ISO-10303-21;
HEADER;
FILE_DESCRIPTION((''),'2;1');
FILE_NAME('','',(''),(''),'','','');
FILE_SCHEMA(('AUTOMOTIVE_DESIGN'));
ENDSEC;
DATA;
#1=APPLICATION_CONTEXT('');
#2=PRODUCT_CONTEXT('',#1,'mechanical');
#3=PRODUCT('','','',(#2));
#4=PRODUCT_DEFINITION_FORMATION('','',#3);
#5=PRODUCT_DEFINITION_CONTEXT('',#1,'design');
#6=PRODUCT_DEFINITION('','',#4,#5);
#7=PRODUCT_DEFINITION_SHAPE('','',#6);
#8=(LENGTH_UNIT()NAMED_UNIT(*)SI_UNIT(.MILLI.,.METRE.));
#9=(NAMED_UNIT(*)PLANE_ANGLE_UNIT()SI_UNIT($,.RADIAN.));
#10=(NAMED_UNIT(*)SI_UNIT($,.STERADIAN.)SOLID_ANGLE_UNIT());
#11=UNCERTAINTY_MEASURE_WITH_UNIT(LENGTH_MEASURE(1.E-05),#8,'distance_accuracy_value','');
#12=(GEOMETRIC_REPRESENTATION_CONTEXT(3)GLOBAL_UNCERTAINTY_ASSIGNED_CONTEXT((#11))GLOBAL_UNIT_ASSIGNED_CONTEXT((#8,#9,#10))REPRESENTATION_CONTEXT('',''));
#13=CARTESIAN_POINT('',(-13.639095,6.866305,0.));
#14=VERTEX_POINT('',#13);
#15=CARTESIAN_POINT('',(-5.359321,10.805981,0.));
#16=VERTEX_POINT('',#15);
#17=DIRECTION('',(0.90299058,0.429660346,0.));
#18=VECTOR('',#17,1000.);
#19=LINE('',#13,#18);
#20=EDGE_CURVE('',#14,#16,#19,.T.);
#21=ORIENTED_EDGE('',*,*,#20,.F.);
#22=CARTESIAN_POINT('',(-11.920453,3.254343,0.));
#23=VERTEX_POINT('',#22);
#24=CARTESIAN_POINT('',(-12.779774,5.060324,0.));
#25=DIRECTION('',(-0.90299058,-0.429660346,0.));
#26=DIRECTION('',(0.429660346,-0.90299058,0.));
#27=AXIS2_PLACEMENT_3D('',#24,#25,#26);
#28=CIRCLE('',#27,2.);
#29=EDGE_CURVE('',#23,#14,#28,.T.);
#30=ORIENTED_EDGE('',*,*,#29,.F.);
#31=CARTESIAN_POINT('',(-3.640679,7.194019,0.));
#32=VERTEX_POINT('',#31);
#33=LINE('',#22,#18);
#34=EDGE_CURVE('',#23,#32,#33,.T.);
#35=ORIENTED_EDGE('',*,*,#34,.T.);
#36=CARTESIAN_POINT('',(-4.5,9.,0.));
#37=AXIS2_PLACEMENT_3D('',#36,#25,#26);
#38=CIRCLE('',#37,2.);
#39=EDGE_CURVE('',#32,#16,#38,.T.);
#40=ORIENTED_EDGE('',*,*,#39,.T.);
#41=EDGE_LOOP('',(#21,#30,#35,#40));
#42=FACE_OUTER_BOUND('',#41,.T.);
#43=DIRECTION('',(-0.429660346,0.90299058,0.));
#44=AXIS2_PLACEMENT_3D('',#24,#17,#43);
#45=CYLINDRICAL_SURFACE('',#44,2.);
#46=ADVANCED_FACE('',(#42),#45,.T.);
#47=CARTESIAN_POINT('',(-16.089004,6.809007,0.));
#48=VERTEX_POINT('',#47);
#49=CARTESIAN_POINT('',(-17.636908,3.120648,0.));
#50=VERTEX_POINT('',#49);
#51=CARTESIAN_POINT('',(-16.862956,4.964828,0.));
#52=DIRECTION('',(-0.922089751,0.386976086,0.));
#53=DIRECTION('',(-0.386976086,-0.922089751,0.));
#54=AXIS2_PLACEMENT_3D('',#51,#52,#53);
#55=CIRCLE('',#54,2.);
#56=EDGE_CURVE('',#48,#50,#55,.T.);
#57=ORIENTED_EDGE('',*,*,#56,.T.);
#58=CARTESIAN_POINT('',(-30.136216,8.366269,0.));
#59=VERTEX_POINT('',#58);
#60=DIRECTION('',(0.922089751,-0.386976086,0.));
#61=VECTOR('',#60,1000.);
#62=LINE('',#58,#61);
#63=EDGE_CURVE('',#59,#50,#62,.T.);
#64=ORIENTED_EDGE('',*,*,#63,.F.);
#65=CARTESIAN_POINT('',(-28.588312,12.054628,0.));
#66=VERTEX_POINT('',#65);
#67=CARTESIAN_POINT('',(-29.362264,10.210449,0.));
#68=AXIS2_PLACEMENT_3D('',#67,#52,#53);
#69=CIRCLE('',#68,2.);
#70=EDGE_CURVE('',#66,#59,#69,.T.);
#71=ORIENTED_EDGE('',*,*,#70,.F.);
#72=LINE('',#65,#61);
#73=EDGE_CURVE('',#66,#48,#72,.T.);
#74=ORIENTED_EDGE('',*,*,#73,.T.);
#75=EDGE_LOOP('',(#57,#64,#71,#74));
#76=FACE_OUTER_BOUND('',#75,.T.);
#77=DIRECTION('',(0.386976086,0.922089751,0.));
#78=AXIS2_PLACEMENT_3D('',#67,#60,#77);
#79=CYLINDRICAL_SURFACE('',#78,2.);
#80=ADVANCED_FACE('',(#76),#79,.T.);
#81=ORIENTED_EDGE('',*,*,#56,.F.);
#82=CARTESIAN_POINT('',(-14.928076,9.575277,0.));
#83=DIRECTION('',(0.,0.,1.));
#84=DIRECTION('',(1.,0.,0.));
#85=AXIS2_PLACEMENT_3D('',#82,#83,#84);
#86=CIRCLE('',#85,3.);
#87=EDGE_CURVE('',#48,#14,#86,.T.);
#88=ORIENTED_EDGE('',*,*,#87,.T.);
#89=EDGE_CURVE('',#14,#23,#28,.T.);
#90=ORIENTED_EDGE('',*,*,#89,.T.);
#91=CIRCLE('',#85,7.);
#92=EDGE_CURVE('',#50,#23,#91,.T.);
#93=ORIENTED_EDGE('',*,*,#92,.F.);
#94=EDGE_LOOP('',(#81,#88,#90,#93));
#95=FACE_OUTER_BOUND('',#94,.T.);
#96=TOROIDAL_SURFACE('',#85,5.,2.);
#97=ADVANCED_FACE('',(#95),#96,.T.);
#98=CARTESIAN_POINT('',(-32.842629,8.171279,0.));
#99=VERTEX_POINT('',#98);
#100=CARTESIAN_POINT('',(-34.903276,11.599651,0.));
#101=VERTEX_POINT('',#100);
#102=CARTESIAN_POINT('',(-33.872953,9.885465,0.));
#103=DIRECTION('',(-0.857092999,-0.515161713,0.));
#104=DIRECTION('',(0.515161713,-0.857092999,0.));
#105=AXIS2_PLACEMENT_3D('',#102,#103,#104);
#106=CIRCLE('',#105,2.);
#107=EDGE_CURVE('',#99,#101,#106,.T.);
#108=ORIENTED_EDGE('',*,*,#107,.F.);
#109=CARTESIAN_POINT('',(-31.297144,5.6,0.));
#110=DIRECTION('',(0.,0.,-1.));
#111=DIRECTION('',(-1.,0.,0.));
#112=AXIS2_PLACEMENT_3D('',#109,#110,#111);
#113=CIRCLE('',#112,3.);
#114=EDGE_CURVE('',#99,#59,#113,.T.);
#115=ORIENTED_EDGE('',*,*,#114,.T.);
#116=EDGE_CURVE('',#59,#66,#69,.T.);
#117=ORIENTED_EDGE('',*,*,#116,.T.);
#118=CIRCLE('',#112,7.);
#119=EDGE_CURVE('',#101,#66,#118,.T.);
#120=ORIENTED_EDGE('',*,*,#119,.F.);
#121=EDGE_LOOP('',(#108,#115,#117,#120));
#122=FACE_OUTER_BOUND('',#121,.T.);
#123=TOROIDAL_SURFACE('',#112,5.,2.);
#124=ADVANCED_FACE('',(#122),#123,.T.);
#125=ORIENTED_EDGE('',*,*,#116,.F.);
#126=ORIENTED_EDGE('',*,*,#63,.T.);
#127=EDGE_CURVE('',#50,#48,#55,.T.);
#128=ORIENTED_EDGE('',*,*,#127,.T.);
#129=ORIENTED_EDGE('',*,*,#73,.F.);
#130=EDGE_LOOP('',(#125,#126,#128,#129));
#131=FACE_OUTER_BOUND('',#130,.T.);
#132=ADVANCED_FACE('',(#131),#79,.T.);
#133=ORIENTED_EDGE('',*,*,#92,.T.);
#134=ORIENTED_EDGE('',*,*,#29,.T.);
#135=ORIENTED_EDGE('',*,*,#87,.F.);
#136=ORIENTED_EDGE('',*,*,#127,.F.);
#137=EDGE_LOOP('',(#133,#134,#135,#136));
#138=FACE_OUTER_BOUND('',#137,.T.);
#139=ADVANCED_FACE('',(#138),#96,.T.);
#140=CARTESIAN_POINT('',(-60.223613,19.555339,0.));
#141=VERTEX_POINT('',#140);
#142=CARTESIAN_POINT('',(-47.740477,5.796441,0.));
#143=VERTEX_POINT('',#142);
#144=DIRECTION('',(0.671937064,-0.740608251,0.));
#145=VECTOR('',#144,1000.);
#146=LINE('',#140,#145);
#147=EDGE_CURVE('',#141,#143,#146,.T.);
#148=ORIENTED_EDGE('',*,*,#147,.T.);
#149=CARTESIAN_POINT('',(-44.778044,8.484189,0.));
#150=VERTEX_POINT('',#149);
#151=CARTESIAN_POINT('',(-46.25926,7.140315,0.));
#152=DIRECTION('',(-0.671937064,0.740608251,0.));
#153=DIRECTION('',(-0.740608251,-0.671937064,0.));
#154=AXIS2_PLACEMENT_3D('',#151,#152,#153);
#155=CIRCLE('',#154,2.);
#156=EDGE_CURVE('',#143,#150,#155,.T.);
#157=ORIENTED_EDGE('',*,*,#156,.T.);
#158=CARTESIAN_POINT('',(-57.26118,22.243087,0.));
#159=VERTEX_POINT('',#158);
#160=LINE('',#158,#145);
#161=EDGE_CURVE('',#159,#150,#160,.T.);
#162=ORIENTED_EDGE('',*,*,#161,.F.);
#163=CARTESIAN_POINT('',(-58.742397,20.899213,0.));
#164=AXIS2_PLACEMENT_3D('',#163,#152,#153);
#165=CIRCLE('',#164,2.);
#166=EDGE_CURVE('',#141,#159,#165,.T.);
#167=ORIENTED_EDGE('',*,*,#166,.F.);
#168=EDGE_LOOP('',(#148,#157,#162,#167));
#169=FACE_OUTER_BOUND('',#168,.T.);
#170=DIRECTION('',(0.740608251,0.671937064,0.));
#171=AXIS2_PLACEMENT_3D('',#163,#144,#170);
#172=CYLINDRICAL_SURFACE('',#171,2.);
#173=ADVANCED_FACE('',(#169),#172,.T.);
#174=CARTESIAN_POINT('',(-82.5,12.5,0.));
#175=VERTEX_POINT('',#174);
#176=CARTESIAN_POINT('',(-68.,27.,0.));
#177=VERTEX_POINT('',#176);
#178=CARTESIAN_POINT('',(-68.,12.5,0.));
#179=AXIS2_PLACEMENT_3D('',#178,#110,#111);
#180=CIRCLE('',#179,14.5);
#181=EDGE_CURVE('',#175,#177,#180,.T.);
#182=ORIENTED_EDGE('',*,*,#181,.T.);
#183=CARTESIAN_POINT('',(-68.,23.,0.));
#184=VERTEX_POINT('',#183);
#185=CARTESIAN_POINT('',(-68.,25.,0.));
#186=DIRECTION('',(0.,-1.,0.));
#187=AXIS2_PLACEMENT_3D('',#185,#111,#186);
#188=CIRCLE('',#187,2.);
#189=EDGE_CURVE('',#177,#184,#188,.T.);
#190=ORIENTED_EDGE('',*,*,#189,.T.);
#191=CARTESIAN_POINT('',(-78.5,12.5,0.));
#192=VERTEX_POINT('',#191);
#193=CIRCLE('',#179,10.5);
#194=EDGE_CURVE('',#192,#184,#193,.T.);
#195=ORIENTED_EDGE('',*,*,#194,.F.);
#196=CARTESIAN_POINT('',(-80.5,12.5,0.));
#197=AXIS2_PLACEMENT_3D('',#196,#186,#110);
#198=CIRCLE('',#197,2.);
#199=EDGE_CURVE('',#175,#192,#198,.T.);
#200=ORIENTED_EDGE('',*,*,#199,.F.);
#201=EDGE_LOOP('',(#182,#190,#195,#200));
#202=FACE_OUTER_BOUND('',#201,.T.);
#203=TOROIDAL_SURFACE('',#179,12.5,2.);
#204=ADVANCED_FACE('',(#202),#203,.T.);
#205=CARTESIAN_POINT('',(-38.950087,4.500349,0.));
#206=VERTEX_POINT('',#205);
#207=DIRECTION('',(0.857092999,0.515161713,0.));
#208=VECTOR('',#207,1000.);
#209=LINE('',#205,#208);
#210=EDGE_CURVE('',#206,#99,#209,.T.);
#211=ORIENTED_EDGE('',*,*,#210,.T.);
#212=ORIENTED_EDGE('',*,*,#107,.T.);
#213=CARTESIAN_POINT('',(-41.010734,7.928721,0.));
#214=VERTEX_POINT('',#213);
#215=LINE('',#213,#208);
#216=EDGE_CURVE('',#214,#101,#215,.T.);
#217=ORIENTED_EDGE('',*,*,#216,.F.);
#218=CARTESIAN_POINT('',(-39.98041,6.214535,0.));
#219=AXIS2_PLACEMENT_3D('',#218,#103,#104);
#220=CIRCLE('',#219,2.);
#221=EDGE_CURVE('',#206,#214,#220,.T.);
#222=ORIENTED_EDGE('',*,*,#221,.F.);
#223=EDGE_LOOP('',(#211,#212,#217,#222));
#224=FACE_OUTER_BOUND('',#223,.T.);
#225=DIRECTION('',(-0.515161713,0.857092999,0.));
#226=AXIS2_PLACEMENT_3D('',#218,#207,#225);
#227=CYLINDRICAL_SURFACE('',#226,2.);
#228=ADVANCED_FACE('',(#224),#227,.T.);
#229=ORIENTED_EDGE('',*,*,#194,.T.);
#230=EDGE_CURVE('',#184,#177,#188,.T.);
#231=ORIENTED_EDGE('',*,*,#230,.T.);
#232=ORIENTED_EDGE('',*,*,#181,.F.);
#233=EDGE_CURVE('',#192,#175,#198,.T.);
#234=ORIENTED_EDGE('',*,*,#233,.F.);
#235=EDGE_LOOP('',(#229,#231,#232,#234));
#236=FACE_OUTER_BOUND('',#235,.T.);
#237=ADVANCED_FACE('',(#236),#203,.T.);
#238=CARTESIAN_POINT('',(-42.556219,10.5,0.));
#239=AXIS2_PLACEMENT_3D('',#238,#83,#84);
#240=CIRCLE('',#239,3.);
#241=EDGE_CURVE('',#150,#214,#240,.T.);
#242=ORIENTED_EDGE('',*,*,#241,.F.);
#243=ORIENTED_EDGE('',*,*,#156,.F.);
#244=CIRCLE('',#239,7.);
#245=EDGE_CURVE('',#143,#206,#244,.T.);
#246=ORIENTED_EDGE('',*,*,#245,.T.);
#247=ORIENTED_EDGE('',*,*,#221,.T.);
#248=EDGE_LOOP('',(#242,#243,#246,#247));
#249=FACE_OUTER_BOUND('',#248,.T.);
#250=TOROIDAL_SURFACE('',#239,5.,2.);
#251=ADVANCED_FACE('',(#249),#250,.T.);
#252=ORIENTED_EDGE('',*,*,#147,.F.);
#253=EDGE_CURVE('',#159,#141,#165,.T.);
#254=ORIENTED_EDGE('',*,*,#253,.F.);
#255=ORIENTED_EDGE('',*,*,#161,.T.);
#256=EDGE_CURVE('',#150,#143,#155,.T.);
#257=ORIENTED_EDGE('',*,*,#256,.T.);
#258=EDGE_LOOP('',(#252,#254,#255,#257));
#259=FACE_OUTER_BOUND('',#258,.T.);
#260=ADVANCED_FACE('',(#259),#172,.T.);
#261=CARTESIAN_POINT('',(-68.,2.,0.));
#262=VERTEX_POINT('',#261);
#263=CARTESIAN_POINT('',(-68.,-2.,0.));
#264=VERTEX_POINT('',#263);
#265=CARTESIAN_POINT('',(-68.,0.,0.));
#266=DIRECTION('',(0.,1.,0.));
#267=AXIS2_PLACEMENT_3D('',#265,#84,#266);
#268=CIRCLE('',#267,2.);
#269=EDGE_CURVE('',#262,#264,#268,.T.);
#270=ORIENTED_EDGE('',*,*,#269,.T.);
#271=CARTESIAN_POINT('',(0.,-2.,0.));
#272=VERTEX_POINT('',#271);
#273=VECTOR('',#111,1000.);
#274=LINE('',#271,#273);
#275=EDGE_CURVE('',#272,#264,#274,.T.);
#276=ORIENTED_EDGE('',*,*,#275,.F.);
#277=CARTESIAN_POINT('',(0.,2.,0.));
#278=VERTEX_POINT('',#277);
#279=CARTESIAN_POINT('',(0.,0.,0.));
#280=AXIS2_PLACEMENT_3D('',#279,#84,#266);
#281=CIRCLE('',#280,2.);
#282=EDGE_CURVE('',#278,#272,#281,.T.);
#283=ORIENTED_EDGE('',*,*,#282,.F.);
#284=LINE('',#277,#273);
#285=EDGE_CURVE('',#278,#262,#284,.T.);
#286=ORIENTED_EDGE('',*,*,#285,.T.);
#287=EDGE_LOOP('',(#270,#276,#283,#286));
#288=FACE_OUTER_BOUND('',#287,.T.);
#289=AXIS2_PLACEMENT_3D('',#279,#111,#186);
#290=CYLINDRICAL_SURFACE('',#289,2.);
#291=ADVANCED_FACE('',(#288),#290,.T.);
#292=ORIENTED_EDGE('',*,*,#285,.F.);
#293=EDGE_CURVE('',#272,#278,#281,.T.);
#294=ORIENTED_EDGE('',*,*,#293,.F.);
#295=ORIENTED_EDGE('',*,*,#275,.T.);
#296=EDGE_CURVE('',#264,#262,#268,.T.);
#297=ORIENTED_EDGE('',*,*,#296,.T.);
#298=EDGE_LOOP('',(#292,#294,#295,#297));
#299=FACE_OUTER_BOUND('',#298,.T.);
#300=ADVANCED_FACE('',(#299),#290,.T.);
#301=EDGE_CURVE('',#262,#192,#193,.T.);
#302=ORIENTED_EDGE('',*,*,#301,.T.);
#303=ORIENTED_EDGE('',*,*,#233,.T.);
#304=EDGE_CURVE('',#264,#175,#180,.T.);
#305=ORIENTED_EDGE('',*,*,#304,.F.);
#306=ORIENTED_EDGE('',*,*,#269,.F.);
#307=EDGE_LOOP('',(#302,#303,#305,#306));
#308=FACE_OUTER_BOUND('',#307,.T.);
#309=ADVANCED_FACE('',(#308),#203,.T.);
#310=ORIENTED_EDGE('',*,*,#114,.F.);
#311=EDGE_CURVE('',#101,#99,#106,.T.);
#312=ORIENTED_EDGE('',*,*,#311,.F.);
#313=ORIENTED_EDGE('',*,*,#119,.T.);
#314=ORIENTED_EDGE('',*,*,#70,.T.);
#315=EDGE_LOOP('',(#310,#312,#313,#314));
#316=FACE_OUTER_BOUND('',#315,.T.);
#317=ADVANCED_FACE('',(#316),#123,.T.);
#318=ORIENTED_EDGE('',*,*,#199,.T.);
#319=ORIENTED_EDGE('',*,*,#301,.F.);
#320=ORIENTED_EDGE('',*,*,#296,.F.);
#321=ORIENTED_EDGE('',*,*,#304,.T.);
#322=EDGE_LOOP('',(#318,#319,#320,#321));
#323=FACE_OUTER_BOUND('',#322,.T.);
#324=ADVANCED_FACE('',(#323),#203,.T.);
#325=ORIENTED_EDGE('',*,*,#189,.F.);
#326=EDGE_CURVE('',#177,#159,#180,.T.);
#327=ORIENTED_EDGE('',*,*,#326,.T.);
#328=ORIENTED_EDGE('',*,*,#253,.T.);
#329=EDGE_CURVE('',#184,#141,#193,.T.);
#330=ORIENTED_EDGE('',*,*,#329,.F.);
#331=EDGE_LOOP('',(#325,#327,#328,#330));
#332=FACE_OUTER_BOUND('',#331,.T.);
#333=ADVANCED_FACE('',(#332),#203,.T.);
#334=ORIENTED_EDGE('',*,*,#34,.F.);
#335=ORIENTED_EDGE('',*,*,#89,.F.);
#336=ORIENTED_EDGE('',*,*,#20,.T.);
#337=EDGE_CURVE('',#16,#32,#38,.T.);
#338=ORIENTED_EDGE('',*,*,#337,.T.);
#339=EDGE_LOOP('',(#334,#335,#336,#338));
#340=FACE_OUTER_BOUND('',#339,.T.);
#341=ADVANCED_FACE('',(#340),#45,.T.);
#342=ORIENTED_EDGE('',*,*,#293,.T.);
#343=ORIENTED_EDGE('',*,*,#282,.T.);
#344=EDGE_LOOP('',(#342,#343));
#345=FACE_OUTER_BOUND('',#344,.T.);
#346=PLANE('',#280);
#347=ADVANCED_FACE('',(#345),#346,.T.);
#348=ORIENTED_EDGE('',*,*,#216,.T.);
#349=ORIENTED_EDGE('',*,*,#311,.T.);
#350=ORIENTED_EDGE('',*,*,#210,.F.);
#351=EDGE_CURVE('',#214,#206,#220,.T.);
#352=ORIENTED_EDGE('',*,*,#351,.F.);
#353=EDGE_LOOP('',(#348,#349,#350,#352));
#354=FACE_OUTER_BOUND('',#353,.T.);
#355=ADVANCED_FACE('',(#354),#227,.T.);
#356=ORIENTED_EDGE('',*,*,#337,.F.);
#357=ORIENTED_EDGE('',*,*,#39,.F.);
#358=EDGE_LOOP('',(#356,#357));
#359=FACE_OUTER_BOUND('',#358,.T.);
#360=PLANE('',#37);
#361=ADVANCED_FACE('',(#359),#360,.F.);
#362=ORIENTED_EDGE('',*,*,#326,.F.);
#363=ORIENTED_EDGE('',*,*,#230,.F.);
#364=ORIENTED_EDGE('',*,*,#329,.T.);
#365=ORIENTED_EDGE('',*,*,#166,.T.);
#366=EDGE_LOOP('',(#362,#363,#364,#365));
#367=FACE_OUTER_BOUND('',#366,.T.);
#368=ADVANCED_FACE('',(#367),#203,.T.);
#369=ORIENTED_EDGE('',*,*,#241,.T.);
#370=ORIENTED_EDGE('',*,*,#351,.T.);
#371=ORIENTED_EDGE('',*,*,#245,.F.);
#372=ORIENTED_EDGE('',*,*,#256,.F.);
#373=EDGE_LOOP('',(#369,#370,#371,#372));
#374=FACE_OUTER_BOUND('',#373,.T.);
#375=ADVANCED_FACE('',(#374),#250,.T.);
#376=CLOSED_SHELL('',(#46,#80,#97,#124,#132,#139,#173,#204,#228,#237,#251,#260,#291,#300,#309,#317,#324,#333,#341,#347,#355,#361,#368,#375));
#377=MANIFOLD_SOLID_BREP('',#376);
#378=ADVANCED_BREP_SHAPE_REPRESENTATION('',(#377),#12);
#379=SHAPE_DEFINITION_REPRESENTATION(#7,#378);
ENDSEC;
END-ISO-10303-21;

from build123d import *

# Parameters (mm, degrees)
WIRE_SWEEP_4_PROFILE_R = 2


with BuildPart() as part:
    # Wire Sweep Ø4: sweep along a path in Clip Wire Path
    with BuildLine(Plane.XY) as wire_sweep_4_path:
        Line((0, 0), (-68, 0))
        ThreePointArc((-68, 0), (-80.5, 12.5), (-68, 25))
        ThreePointArc((-68, 25), (-62.93740019, 23.928914347), (-58.742396863, 20.899213306))
        Line((-58.742396863, 20.899213306), (-46.259260276, 7.140314678))
        ThreePointArc((-46.259260276, 7.140314678), (-43.2855546, 5.553479039), (-39.980410457, 6.214535003))
        Line((-39.980410457, 6.214535003), (-33.8729527, 9.885464997))
        ThreePointArc((-33.8729527, 9.885464997), (-31.656450173, 10.587073207), (-29.362263704, 10.210448754))
        Line((-29.362263704, 10.210448754), (-16.862956001, 4.964827953))
        ThreePointArc((-16.862956001, 4.964827953), (-14.811169509, 4.576643597), (-12.779773841, 5.060323807))
        Line((-12.779773841, 5.060323807), (-4.5, 9))
    # Wire Sweep Ø4 profile (on start of the path) → Wire Sweep Ø4 (sweep)
    with BuildSketch(Plane(origin=(0, 0, 0), x_dir=(0, -1, 0), z_dir=(-1, 0, 0))):
        Circle(WIRE_SWEEP_4_PROFILE_R)
    sweep(path=wire_sweep_4_path.line)


solid = part.part
